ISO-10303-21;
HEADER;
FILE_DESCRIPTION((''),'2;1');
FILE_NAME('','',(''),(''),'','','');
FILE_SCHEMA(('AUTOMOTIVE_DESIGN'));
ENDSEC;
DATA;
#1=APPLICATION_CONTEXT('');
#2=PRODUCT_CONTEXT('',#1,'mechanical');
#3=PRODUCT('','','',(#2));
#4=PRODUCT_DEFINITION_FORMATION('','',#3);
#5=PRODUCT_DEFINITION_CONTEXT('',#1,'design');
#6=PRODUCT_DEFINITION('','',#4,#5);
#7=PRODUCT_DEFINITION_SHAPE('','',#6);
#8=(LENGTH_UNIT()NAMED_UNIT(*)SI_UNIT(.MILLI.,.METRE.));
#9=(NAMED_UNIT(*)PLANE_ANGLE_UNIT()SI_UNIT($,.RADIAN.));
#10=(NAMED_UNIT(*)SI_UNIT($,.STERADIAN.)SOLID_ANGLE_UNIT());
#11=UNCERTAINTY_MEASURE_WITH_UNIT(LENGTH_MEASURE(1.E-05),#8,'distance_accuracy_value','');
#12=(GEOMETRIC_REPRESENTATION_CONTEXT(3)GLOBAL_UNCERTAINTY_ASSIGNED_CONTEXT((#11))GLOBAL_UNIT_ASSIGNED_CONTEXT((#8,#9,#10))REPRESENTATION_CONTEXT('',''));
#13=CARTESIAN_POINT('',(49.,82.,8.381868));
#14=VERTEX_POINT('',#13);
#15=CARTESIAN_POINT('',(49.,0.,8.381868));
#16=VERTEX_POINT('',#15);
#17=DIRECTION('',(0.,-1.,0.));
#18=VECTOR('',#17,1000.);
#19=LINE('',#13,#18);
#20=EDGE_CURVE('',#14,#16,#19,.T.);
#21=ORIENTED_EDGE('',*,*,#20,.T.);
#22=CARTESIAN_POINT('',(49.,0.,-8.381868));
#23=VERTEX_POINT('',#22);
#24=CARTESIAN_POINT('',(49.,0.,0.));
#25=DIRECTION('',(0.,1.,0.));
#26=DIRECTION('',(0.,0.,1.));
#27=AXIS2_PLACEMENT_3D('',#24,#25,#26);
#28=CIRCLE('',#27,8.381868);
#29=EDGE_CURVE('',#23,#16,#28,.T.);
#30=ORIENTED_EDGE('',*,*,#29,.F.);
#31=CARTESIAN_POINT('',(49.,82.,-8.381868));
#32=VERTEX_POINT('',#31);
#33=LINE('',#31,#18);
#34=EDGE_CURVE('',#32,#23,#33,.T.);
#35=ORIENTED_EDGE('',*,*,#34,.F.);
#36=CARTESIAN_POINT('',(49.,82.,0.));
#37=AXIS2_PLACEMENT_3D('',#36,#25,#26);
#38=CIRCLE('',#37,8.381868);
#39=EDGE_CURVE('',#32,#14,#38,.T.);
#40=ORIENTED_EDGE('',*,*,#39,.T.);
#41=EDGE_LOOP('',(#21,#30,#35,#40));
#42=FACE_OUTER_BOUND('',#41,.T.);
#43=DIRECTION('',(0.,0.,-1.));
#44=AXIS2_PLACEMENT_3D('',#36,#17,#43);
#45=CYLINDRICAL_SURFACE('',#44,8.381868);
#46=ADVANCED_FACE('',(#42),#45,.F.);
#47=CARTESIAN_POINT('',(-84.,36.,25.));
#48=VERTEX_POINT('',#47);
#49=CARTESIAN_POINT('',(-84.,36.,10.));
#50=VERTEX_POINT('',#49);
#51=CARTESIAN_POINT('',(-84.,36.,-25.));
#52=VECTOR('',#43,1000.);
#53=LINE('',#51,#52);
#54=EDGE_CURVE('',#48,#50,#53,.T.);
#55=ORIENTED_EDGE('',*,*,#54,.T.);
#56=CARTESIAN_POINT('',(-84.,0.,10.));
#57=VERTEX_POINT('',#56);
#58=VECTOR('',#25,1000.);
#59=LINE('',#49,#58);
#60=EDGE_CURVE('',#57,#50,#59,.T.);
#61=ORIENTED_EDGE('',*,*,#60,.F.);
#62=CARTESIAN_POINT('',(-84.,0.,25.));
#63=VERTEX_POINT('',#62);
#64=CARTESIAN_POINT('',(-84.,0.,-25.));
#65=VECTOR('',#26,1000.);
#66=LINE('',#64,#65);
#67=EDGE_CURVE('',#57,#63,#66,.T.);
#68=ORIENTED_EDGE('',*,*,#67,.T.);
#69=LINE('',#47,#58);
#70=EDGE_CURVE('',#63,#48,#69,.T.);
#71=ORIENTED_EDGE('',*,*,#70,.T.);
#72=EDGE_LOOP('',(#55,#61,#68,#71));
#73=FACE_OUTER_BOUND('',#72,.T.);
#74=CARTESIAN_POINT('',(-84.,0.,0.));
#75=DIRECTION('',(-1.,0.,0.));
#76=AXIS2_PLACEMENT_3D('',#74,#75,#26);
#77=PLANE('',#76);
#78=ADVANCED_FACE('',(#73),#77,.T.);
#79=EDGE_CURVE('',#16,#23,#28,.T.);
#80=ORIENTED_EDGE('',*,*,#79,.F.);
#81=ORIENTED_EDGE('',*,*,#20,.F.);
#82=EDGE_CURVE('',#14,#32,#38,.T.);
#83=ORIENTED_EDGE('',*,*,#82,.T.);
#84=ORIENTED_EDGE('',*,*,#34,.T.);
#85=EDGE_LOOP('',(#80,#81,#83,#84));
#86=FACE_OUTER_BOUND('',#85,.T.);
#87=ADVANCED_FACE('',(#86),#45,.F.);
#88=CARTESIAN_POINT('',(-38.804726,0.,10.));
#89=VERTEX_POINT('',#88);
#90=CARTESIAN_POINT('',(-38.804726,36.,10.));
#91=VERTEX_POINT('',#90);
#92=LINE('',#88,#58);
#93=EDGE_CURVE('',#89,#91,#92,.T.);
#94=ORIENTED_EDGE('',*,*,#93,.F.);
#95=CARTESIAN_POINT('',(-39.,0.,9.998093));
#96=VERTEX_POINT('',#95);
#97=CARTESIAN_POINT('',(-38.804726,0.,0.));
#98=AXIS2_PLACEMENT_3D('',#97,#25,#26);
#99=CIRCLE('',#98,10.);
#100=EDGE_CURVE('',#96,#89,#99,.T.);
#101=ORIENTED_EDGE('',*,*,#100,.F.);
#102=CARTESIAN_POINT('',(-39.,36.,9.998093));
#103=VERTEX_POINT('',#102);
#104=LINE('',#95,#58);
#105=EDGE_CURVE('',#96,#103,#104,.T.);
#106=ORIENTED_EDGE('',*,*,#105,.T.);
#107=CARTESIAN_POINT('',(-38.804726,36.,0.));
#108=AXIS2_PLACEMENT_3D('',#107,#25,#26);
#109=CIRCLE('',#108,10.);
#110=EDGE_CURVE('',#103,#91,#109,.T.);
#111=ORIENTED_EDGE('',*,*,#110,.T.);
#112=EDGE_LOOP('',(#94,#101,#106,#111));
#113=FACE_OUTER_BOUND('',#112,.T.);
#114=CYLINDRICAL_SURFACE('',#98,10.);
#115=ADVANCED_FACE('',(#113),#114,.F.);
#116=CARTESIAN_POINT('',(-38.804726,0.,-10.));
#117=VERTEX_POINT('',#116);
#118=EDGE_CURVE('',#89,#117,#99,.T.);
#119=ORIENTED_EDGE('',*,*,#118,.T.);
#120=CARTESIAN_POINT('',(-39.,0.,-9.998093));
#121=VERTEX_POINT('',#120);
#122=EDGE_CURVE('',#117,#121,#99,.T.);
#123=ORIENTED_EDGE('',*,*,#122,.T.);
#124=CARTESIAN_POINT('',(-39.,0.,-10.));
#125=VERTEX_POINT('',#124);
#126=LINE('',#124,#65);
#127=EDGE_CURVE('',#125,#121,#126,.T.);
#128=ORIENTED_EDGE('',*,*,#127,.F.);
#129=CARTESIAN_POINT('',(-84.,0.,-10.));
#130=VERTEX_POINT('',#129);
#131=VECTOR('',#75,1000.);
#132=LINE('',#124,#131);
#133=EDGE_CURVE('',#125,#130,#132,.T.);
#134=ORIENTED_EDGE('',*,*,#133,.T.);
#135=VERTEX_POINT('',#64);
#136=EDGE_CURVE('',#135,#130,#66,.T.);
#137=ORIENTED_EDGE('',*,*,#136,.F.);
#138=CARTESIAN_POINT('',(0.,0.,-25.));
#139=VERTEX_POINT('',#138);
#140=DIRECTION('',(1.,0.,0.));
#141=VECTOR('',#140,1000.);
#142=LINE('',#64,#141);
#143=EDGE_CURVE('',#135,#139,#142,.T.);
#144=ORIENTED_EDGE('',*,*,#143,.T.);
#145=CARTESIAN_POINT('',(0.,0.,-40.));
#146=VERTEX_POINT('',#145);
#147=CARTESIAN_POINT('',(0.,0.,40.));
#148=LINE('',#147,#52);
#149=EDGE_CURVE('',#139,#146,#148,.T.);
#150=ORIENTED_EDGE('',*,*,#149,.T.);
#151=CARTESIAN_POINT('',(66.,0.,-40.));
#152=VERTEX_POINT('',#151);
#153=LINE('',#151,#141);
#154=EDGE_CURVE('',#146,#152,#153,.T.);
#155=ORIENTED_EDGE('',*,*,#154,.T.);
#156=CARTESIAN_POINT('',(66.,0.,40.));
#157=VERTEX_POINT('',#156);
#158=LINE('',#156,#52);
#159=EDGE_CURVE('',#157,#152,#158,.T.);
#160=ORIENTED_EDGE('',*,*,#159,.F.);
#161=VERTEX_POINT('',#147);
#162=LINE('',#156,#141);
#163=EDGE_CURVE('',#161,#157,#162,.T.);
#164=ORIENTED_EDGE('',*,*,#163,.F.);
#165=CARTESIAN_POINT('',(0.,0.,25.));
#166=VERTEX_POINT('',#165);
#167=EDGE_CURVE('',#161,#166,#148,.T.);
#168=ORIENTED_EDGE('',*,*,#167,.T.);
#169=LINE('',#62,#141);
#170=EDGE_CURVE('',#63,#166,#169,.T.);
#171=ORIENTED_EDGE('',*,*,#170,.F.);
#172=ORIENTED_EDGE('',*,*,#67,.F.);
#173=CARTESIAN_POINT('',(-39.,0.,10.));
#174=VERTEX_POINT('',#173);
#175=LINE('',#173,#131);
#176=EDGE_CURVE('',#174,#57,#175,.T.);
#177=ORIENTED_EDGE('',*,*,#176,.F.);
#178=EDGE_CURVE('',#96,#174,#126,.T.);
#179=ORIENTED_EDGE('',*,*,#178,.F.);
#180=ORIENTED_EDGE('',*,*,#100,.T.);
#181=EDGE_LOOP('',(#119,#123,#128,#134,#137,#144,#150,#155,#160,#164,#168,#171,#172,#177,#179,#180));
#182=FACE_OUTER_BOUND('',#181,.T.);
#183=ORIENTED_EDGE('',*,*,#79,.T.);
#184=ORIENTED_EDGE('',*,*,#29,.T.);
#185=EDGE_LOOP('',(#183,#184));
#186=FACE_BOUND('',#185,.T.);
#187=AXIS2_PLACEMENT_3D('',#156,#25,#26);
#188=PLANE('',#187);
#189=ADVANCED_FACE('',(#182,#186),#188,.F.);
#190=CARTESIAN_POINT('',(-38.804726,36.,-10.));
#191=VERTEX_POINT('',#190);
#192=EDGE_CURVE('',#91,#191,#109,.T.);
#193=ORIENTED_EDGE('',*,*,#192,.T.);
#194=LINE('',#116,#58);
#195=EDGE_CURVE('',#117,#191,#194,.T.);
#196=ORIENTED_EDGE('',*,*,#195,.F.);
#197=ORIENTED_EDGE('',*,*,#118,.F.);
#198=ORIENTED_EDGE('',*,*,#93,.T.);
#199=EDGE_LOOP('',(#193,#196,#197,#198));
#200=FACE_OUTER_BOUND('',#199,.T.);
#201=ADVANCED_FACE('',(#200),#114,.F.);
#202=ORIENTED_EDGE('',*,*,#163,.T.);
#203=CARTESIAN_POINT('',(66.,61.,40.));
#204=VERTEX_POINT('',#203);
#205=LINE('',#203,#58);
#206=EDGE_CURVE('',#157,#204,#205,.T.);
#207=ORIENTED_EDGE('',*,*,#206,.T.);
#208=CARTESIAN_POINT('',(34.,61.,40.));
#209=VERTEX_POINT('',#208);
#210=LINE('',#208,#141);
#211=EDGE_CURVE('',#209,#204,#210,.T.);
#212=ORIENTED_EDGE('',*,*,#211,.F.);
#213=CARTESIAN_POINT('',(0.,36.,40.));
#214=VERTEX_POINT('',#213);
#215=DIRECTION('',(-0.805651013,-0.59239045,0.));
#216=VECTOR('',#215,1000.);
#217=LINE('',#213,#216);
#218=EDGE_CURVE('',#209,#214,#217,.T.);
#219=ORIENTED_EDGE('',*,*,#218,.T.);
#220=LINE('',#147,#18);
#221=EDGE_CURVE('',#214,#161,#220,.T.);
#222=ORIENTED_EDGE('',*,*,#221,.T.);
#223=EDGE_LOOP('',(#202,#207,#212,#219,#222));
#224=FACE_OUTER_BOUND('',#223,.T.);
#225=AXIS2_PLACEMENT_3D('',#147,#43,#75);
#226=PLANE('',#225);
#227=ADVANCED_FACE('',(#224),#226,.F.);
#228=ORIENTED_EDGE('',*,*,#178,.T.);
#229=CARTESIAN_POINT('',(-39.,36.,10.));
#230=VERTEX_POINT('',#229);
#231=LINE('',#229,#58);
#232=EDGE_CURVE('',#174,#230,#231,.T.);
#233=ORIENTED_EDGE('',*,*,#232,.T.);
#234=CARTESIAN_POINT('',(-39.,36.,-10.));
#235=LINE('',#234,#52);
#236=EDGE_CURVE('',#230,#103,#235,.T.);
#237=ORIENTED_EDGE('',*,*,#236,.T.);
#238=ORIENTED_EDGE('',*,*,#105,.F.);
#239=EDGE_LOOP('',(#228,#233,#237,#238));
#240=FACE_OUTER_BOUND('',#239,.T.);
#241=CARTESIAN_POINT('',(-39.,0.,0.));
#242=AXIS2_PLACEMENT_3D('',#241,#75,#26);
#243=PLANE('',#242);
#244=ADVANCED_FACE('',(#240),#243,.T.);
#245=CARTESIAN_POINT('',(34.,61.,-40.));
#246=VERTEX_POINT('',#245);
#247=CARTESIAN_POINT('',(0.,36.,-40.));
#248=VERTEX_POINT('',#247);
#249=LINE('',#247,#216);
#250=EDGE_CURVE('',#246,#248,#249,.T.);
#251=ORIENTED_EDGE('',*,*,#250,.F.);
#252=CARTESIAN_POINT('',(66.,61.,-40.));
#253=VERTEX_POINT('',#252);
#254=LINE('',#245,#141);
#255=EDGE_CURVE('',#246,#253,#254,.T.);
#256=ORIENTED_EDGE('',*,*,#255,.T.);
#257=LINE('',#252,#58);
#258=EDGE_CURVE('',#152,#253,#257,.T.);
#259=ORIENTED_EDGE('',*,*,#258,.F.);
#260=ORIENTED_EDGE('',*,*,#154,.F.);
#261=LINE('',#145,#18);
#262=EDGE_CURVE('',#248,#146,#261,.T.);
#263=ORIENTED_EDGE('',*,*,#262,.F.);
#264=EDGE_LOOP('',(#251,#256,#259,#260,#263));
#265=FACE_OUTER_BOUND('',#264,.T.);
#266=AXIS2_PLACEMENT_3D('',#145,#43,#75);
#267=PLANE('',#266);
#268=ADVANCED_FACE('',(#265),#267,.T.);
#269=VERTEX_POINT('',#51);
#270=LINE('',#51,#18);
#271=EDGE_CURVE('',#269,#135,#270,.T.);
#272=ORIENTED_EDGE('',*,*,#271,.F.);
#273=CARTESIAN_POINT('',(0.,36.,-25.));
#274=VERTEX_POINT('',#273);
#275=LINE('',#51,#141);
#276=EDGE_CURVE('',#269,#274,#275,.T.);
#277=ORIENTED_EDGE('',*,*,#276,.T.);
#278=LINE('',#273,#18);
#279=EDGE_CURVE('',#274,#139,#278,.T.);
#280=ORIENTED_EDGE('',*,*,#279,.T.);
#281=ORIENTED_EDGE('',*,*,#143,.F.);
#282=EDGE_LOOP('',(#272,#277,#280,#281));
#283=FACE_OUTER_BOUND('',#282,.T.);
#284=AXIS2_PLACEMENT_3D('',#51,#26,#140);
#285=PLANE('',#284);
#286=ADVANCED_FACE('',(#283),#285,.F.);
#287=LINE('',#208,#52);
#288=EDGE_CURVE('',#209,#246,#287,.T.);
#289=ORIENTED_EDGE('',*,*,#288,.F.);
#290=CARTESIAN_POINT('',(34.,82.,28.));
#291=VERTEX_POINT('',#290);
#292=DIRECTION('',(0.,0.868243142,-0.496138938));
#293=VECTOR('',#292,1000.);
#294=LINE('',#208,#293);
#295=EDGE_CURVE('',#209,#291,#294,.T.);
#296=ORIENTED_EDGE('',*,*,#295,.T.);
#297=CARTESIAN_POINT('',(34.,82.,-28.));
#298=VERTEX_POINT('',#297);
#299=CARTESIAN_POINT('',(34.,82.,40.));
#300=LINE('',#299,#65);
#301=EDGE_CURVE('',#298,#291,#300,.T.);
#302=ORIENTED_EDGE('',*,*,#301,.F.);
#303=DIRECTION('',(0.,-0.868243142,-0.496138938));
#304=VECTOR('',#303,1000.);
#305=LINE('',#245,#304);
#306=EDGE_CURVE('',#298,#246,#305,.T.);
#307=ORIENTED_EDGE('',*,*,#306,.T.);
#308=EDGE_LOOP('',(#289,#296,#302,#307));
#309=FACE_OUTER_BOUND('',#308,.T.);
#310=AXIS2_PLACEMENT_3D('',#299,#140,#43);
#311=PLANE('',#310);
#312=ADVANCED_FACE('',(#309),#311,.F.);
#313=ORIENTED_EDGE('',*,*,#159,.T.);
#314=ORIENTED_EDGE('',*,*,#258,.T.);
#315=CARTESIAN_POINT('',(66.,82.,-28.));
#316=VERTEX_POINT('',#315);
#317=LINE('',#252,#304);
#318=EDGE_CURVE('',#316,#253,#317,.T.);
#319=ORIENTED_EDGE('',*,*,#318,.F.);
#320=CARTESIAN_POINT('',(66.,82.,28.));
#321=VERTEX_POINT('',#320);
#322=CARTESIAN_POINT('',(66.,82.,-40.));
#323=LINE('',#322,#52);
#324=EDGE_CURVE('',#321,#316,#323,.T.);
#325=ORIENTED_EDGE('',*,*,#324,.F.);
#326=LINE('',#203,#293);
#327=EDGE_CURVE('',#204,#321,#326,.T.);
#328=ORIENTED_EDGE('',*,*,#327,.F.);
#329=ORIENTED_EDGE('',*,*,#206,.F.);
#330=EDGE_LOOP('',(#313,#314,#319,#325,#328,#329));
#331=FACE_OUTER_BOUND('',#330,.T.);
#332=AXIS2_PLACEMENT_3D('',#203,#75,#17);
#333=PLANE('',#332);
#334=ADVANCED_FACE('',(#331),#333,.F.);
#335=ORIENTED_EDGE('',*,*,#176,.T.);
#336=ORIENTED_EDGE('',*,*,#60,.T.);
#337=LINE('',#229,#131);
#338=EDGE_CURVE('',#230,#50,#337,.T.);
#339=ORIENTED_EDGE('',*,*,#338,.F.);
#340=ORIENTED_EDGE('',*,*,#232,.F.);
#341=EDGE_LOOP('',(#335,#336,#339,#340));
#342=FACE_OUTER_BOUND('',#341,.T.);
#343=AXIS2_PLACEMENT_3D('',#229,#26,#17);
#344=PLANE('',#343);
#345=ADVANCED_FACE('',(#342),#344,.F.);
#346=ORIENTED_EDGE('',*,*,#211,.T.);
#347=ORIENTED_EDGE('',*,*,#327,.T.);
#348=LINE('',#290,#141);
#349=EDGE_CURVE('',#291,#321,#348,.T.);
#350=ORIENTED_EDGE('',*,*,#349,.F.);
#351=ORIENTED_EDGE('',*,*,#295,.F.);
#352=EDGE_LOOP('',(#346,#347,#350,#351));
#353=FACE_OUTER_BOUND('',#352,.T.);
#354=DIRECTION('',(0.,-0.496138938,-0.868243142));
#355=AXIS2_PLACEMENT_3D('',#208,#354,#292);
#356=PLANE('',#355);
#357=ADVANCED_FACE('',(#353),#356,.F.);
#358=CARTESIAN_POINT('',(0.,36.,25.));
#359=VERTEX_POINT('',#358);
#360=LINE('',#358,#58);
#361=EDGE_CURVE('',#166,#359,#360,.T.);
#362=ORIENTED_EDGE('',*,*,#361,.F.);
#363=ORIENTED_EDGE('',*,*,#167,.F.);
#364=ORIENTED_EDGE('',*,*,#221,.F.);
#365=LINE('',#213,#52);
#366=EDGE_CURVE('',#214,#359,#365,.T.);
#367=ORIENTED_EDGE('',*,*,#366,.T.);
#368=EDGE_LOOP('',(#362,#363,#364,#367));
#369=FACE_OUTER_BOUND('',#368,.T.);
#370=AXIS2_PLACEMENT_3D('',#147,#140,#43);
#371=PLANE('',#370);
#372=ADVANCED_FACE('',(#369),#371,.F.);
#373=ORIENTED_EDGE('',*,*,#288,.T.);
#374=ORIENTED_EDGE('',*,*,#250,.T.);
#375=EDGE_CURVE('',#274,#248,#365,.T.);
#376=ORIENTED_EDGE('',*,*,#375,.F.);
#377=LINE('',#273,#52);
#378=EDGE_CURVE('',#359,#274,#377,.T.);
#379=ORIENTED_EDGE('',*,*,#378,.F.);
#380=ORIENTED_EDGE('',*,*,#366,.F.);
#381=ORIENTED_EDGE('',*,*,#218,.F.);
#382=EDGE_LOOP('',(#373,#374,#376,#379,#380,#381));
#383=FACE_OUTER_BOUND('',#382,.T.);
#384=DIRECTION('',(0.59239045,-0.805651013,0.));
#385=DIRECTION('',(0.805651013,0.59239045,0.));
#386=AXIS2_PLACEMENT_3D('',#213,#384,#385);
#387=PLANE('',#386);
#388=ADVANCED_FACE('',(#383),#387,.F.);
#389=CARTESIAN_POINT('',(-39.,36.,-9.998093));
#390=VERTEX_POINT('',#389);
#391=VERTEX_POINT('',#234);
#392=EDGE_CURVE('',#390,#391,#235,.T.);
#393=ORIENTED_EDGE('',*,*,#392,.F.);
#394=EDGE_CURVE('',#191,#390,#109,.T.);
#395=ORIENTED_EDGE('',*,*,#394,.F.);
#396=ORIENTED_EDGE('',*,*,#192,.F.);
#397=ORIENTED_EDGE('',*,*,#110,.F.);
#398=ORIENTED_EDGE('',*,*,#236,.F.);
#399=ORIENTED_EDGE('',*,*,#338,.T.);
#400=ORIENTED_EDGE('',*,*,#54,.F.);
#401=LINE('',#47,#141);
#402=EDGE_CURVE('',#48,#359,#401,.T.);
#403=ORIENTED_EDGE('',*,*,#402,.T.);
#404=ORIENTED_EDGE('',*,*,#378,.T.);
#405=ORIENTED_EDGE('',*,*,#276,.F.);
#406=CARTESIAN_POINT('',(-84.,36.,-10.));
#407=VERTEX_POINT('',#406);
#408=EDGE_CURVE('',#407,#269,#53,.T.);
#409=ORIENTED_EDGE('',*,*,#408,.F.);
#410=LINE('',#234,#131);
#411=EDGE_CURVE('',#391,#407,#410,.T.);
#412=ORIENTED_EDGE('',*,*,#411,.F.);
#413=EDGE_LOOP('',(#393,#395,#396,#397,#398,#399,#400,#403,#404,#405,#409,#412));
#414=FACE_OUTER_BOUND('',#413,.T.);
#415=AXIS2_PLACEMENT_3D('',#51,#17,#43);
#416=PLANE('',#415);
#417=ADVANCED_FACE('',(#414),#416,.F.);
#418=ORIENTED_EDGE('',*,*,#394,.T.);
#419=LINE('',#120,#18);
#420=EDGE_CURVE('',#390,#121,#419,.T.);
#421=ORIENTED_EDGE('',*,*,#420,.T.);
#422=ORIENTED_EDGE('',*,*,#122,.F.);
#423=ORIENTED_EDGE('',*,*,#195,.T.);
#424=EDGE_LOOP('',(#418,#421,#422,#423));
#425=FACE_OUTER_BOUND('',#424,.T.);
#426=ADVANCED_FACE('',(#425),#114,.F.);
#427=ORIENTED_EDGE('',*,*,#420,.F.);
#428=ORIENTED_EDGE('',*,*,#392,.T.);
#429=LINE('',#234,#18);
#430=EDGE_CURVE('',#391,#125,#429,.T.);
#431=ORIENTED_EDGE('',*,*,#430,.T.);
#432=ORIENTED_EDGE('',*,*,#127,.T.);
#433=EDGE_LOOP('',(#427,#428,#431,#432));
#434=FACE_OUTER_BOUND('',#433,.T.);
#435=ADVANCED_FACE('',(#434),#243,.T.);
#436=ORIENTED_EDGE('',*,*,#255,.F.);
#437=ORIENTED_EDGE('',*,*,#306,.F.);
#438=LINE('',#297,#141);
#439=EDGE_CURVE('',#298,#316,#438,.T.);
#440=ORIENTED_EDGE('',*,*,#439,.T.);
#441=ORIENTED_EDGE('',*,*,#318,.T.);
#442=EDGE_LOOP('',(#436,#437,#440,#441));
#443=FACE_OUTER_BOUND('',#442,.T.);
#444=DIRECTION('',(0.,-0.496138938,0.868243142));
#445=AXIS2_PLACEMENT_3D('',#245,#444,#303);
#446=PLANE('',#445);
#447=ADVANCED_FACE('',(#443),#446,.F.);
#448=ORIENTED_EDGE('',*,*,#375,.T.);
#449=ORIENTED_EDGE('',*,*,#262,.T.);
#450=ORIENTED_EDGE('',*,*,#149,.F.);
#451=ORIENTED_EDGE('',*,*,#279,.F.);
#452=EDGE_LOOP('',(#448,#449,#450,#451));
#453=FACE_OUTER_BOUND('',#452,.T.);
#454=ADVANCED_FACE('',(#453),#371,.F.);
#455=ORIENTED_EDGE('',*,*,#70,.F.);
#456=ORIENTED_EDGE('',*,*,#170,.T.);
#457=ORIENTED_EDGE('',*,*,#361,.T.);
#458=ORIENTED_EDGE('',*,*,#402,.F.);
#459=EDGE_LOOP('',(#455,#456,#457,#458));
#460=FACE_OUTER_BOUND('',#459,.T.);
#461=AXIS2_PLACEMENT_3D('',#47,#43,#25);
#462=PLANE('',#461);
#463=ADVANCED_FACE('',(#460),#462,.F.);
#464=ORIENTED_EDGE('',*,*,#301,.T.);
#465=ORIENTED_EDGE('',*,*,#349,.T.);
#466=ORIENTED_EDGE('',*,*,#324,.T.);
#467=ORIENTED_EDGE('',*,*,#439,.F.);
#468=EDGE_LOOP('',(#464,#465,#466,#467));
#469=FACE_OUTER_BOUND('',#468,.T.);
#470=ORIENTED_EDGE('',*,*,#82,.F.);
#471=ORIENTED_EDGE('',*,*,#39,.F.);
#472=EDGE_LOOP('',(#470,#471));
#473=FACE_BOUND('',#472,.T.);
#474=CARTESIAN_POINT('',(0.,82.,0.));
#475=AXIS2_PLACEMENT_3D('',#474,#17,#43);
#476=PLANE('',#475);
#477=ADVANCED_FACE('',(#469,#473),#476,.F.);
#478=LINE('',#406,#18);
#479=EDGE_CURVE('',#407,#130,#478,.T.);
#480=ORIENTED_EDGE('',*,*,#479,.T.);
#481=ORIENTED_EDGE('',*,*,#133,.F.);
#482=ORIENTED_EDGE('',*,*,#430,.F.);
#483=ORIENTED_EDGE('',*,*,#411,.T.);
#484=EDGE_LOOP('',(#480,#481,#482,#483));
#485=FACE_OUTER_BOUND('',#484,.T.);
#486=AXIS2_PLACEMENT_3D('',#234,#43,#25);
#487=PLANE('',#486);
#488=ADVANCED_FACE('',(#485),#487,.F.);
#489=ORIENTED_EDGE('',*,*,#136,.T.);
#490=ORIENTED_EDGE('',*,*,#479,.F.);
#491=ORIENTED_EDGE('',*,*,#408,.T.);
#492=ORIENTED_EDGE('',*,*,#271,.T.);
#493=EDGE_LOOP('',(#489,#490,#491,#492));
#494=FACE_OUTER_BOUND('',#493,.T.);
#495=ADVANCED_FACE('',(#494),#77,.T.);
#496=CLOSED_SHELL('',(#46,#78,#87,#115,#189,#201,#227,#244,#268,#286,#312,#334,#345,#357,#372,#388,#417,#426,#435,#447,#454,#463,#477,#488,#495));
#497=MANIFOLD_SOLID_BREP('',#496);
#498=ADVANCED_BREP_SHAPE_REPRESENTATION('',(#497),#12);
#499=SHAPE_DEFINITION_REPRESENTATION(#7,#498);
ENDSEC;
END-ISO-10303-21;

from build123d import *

# Parameters (mm, degrees)
BASE_BLOCK_DEPTH         = 40
TOP_BOSS_PROFILE_W       = 32
TOP_BOSS_PROFILE_H       = 80
TOP_BOSS_PROFILE_R       = 8.381868302
TOP_BOSS_DEPTH           = 21
U_SLOT_W12_DEPTH         = 32
ARM_PROFILE_W            = 50
ARM_PROFILE_H            = 36
ARM_DEPTH                = 84
SQUARE_NOTCH_PROFILE_W   = 20
SQUARE_NOTCH_PROFILE_H   = 36
SQUARE_NOTCH_15X15_DEPTH = 45
ARM_CUT_PROFILE_R        = 10
ARM_CUT_DEPTH            = 36
HOLE_SKETCH_R            = 8.381868302
HOLE_DEPTH               = 125.016127983


with BuildPart() as part:
    # Base Block Profile → Base Block (new, symmetric)
    with BuildSketch(Plane.XY):
        Polygon((0, 0), (0, 36), (34, 61), (66, 61), (66, 0), align=None)
    extrude(amount=BASE_BLOCK_DEPTH, both=True)

    # Top Boss Profile → Top Boss (add)
    with BuildSketch(Plane(origin=(0, 61, 0), x_dir=(1, 0, 0), z_dir=(0, 1, 0))):
        with Locations((50, 0)):
            Rectangle(TOP_BOSS_PROFILE_W, TOP_BOSS_PROFILE_H)
        with Locations(Location((49, 0, 0), (0, 0, 90))):
            Circle(TOP_BOSS_PROFILE_R, mode=Mode.SUBTRACT)
    extrude(amount=TOP_BOSS_DEPTH)

    # U-Slot Profile → U-Slot W12 (cut)
    with BuildSketch(Plane(origin=(66, 0, 0), x_dir=(0, 0, -1), z_dir=(1, 0, 0))):
        Polygon((-40, 82), (-28, 82), (-40, 61), align=None)
        Polygon((40, 61), (28, 82), (40, 82), align=None)
    extrude(amount=-U_SLOT_W12_DEPTH, mode=Mode.SUBTRACT)

    # Arm Profile → Arm (add)
    with BuildSketch(Plane.ZY):
        with Locations((0, 18)):
            Rectangle(ARM_PROFILE_W, ARM_PROFILE_H)
    extrude(amount=ARM_DEPTH)

    # Square Notch Profile → Square Notch 15x15 (cut)
    with BuildSketch(Plane.ZY.offset(84)):
        with Locations((0, 18)):
            Rectangle(SQUARE_NOTCH_PROFILE_W, SQUARE_NOTCH_PROFILE_H)
    extrude(amount=-SQUARE_NOTCH_15X15_DEPTH, mode=Mode.SUBTRACT)

    # Arm Cut Profile → Arm Cut (cut)
    with BuildSketch(Plane(origin=(0, 36, 0), x_dir=(1, 0, 0), z_dir=(0, 1, 0))):
        with Locations((-38.804725968, 0)):
            Circle(ARM_CUT_PROFILE_R)
    extrude(amount=-ARM_CUT_DEPTH, mode=Mode.SUBTRACT)

    # Hole Sketch → Hole (cut, through all)
    with BuildSketch(Plane(origin=(0, 82, 0), x_dir=(1, 0, 0), z_dir=(0, 1, 0))):
        with Locations(Location((49, 0, 0), (0, 0, 90))):
            Circle(HOLE_SKETCH_R)
    extrude(amount=-HOLE_DEPTH, mode=Mode.SUBTRACT)


solid = part.part
